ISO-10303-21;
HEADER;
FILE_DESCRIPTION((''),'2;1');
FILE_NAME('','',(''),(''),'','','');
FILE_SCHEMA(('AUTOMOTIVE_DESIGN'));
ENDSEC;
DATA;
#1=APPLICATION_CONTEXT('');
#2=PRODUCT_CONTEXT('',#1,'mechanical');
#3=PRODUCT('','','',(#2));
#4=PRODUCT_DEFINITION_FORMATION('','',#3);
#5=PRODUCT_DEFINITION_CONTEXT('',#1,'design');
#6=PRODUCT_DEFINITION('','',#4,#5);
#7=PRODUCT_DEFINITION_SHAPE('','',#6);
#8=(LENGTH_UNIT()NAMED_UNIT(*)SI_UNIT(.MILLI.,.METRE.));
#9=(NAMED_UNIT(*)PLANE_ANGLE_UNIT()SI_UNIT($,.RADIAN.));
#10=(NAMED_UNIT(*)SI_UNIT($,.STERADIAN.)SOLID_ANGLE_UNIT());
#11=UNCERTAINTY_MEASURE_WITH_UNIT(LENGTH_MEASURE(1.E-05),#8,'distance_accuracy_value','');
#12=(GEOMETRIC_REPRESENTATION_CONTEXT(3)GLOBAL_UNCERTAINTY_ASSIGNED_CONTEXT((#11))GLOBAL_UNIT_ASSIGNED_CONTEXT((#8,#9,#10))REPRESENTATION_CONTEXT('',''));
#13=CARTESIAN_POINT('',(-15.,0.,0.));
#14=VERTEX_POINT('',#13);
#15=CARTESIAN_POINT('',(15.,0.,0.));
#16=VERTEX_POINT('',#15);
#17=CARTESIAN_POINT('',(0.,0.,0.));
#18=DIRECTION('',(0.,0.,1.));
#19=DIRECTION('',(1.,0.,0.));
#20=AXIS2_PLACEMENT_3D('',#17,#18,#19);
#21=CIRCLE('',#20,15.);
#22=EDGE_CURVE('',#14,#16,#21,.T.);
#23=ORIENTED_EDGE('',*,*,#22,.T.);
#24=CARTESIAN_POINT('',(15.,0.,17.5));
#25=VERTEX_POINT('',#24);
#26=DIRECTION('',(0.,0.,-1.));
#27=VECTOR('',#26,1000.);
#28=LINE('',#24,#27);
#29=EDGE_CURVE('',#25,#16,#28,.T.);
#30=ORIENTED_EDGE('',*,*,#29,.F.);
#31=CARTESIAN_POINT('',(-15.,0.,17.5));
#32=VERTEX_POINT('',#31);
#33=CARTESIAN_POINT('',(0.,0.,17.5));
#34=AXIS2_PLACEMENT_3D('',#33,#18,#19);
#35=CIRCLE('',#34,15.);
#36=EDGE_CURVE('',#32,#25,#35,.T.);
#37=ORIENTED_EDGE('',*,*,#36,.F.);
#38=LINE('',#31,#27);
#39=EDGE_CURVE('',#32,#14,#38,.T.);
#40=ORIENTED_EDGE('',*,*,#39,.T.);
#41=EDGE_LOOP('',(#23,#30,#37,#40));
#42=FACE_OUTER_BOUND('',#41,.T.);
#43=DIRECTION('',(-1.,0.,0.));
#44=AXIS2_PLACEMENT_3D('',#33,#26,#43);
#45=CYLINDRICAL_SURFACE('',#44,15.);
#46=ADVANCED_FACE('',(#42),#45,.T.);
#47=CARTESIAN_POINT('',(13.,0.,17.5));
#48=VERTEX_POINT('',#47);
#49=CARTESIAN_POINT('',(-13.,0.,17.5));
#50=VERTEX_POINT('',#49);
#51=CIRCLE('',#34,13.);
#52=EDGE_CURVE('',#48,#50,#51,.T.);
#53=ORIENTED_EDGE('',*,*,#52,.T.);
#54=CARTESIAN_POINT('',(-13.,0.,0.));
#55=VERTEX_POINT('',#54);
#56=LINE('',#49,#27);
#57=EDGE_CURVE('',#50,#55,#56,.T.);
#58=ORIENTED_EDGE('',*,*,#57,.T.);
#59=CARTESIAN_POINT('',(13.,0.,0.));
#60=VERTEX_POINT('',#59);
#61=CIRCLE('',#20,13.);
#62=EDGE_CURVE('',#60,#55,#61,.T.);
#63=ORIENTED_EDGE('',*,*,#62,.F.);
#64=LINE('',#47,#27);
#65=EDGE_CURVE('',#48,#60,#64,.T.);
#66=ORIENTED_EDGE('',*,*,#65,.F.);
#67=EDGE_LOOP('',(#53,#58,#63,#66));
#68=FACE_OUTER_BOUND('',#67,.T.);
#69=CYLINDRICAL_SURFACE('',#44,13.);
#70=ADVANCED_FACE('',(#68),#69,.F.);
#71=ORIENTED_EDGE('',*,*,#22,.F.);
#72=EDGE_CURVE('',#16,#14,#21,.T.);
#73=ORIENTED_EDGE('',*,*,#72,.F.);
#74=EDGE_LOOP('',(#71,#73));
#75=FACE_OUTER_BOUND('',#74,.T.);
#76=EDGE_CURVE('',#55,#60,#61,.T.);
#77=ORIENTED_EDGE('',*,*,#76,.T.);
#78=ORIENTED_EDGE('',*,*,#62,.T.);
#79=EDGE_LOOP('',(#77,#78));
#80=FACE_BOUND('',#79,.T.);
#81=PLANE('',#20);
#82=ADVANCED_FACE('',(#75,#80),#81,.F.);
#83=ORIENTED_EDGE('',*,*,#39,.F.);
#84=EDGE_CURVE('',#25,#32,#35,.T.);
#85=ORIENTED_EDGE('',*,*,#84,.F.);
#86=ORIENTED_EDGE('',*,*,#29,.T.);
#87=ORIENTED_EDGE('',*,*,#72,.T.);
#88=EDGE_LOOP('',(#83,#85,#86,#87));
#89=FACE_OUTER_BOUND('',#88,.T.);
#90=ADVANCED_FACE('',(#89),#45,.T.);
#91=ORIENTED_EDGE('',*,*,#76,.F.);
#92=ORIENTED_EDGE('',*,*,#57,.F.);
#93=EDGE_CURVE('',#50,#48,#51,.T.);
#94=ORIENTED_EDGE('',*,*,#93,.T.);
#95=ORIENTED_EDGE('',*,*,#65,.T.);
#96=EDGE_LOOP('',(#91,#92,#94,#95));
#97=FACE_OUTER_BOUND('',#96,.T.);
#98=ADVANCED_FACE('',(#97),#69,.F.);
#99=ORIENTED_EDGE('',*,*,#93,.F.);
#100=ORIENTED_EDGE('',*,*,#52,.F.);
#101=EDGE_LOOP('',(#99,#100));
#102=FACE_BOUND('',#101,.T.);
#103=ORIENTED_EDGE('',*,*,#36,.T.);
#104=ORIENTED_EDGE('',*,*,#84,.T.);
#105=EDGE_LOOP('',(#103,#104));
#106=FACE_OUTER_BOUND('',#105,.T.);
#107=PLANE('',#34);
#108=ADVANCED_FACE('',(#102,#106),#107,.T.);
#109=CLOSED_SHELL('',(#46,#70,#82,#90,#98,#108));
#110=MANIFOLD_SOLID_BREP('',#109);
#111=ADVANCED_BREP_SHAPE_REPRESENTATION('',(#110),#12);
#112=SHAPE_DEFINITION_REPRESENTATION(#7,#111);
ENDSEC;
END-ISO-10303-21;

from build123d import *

# Parameters (mm, degrees)
SKETCH1_R           = 15
SKETCH1_R_2         = 13
BOSS_EXTRUDE1_DEPTH = 17.5


with BuildPart() as part:
    # Sketch1 → Boss-Extrude1 (new body)
    with BuildSketch(Plane.XY):
        Circle(SKETCH1_R)
        Circle(SKETCH1_R_2, mode=Mode.SUBTRACT)
    extrude(amount=BOSS_EXTRUDE1_DEPTH)


solid = part.part
